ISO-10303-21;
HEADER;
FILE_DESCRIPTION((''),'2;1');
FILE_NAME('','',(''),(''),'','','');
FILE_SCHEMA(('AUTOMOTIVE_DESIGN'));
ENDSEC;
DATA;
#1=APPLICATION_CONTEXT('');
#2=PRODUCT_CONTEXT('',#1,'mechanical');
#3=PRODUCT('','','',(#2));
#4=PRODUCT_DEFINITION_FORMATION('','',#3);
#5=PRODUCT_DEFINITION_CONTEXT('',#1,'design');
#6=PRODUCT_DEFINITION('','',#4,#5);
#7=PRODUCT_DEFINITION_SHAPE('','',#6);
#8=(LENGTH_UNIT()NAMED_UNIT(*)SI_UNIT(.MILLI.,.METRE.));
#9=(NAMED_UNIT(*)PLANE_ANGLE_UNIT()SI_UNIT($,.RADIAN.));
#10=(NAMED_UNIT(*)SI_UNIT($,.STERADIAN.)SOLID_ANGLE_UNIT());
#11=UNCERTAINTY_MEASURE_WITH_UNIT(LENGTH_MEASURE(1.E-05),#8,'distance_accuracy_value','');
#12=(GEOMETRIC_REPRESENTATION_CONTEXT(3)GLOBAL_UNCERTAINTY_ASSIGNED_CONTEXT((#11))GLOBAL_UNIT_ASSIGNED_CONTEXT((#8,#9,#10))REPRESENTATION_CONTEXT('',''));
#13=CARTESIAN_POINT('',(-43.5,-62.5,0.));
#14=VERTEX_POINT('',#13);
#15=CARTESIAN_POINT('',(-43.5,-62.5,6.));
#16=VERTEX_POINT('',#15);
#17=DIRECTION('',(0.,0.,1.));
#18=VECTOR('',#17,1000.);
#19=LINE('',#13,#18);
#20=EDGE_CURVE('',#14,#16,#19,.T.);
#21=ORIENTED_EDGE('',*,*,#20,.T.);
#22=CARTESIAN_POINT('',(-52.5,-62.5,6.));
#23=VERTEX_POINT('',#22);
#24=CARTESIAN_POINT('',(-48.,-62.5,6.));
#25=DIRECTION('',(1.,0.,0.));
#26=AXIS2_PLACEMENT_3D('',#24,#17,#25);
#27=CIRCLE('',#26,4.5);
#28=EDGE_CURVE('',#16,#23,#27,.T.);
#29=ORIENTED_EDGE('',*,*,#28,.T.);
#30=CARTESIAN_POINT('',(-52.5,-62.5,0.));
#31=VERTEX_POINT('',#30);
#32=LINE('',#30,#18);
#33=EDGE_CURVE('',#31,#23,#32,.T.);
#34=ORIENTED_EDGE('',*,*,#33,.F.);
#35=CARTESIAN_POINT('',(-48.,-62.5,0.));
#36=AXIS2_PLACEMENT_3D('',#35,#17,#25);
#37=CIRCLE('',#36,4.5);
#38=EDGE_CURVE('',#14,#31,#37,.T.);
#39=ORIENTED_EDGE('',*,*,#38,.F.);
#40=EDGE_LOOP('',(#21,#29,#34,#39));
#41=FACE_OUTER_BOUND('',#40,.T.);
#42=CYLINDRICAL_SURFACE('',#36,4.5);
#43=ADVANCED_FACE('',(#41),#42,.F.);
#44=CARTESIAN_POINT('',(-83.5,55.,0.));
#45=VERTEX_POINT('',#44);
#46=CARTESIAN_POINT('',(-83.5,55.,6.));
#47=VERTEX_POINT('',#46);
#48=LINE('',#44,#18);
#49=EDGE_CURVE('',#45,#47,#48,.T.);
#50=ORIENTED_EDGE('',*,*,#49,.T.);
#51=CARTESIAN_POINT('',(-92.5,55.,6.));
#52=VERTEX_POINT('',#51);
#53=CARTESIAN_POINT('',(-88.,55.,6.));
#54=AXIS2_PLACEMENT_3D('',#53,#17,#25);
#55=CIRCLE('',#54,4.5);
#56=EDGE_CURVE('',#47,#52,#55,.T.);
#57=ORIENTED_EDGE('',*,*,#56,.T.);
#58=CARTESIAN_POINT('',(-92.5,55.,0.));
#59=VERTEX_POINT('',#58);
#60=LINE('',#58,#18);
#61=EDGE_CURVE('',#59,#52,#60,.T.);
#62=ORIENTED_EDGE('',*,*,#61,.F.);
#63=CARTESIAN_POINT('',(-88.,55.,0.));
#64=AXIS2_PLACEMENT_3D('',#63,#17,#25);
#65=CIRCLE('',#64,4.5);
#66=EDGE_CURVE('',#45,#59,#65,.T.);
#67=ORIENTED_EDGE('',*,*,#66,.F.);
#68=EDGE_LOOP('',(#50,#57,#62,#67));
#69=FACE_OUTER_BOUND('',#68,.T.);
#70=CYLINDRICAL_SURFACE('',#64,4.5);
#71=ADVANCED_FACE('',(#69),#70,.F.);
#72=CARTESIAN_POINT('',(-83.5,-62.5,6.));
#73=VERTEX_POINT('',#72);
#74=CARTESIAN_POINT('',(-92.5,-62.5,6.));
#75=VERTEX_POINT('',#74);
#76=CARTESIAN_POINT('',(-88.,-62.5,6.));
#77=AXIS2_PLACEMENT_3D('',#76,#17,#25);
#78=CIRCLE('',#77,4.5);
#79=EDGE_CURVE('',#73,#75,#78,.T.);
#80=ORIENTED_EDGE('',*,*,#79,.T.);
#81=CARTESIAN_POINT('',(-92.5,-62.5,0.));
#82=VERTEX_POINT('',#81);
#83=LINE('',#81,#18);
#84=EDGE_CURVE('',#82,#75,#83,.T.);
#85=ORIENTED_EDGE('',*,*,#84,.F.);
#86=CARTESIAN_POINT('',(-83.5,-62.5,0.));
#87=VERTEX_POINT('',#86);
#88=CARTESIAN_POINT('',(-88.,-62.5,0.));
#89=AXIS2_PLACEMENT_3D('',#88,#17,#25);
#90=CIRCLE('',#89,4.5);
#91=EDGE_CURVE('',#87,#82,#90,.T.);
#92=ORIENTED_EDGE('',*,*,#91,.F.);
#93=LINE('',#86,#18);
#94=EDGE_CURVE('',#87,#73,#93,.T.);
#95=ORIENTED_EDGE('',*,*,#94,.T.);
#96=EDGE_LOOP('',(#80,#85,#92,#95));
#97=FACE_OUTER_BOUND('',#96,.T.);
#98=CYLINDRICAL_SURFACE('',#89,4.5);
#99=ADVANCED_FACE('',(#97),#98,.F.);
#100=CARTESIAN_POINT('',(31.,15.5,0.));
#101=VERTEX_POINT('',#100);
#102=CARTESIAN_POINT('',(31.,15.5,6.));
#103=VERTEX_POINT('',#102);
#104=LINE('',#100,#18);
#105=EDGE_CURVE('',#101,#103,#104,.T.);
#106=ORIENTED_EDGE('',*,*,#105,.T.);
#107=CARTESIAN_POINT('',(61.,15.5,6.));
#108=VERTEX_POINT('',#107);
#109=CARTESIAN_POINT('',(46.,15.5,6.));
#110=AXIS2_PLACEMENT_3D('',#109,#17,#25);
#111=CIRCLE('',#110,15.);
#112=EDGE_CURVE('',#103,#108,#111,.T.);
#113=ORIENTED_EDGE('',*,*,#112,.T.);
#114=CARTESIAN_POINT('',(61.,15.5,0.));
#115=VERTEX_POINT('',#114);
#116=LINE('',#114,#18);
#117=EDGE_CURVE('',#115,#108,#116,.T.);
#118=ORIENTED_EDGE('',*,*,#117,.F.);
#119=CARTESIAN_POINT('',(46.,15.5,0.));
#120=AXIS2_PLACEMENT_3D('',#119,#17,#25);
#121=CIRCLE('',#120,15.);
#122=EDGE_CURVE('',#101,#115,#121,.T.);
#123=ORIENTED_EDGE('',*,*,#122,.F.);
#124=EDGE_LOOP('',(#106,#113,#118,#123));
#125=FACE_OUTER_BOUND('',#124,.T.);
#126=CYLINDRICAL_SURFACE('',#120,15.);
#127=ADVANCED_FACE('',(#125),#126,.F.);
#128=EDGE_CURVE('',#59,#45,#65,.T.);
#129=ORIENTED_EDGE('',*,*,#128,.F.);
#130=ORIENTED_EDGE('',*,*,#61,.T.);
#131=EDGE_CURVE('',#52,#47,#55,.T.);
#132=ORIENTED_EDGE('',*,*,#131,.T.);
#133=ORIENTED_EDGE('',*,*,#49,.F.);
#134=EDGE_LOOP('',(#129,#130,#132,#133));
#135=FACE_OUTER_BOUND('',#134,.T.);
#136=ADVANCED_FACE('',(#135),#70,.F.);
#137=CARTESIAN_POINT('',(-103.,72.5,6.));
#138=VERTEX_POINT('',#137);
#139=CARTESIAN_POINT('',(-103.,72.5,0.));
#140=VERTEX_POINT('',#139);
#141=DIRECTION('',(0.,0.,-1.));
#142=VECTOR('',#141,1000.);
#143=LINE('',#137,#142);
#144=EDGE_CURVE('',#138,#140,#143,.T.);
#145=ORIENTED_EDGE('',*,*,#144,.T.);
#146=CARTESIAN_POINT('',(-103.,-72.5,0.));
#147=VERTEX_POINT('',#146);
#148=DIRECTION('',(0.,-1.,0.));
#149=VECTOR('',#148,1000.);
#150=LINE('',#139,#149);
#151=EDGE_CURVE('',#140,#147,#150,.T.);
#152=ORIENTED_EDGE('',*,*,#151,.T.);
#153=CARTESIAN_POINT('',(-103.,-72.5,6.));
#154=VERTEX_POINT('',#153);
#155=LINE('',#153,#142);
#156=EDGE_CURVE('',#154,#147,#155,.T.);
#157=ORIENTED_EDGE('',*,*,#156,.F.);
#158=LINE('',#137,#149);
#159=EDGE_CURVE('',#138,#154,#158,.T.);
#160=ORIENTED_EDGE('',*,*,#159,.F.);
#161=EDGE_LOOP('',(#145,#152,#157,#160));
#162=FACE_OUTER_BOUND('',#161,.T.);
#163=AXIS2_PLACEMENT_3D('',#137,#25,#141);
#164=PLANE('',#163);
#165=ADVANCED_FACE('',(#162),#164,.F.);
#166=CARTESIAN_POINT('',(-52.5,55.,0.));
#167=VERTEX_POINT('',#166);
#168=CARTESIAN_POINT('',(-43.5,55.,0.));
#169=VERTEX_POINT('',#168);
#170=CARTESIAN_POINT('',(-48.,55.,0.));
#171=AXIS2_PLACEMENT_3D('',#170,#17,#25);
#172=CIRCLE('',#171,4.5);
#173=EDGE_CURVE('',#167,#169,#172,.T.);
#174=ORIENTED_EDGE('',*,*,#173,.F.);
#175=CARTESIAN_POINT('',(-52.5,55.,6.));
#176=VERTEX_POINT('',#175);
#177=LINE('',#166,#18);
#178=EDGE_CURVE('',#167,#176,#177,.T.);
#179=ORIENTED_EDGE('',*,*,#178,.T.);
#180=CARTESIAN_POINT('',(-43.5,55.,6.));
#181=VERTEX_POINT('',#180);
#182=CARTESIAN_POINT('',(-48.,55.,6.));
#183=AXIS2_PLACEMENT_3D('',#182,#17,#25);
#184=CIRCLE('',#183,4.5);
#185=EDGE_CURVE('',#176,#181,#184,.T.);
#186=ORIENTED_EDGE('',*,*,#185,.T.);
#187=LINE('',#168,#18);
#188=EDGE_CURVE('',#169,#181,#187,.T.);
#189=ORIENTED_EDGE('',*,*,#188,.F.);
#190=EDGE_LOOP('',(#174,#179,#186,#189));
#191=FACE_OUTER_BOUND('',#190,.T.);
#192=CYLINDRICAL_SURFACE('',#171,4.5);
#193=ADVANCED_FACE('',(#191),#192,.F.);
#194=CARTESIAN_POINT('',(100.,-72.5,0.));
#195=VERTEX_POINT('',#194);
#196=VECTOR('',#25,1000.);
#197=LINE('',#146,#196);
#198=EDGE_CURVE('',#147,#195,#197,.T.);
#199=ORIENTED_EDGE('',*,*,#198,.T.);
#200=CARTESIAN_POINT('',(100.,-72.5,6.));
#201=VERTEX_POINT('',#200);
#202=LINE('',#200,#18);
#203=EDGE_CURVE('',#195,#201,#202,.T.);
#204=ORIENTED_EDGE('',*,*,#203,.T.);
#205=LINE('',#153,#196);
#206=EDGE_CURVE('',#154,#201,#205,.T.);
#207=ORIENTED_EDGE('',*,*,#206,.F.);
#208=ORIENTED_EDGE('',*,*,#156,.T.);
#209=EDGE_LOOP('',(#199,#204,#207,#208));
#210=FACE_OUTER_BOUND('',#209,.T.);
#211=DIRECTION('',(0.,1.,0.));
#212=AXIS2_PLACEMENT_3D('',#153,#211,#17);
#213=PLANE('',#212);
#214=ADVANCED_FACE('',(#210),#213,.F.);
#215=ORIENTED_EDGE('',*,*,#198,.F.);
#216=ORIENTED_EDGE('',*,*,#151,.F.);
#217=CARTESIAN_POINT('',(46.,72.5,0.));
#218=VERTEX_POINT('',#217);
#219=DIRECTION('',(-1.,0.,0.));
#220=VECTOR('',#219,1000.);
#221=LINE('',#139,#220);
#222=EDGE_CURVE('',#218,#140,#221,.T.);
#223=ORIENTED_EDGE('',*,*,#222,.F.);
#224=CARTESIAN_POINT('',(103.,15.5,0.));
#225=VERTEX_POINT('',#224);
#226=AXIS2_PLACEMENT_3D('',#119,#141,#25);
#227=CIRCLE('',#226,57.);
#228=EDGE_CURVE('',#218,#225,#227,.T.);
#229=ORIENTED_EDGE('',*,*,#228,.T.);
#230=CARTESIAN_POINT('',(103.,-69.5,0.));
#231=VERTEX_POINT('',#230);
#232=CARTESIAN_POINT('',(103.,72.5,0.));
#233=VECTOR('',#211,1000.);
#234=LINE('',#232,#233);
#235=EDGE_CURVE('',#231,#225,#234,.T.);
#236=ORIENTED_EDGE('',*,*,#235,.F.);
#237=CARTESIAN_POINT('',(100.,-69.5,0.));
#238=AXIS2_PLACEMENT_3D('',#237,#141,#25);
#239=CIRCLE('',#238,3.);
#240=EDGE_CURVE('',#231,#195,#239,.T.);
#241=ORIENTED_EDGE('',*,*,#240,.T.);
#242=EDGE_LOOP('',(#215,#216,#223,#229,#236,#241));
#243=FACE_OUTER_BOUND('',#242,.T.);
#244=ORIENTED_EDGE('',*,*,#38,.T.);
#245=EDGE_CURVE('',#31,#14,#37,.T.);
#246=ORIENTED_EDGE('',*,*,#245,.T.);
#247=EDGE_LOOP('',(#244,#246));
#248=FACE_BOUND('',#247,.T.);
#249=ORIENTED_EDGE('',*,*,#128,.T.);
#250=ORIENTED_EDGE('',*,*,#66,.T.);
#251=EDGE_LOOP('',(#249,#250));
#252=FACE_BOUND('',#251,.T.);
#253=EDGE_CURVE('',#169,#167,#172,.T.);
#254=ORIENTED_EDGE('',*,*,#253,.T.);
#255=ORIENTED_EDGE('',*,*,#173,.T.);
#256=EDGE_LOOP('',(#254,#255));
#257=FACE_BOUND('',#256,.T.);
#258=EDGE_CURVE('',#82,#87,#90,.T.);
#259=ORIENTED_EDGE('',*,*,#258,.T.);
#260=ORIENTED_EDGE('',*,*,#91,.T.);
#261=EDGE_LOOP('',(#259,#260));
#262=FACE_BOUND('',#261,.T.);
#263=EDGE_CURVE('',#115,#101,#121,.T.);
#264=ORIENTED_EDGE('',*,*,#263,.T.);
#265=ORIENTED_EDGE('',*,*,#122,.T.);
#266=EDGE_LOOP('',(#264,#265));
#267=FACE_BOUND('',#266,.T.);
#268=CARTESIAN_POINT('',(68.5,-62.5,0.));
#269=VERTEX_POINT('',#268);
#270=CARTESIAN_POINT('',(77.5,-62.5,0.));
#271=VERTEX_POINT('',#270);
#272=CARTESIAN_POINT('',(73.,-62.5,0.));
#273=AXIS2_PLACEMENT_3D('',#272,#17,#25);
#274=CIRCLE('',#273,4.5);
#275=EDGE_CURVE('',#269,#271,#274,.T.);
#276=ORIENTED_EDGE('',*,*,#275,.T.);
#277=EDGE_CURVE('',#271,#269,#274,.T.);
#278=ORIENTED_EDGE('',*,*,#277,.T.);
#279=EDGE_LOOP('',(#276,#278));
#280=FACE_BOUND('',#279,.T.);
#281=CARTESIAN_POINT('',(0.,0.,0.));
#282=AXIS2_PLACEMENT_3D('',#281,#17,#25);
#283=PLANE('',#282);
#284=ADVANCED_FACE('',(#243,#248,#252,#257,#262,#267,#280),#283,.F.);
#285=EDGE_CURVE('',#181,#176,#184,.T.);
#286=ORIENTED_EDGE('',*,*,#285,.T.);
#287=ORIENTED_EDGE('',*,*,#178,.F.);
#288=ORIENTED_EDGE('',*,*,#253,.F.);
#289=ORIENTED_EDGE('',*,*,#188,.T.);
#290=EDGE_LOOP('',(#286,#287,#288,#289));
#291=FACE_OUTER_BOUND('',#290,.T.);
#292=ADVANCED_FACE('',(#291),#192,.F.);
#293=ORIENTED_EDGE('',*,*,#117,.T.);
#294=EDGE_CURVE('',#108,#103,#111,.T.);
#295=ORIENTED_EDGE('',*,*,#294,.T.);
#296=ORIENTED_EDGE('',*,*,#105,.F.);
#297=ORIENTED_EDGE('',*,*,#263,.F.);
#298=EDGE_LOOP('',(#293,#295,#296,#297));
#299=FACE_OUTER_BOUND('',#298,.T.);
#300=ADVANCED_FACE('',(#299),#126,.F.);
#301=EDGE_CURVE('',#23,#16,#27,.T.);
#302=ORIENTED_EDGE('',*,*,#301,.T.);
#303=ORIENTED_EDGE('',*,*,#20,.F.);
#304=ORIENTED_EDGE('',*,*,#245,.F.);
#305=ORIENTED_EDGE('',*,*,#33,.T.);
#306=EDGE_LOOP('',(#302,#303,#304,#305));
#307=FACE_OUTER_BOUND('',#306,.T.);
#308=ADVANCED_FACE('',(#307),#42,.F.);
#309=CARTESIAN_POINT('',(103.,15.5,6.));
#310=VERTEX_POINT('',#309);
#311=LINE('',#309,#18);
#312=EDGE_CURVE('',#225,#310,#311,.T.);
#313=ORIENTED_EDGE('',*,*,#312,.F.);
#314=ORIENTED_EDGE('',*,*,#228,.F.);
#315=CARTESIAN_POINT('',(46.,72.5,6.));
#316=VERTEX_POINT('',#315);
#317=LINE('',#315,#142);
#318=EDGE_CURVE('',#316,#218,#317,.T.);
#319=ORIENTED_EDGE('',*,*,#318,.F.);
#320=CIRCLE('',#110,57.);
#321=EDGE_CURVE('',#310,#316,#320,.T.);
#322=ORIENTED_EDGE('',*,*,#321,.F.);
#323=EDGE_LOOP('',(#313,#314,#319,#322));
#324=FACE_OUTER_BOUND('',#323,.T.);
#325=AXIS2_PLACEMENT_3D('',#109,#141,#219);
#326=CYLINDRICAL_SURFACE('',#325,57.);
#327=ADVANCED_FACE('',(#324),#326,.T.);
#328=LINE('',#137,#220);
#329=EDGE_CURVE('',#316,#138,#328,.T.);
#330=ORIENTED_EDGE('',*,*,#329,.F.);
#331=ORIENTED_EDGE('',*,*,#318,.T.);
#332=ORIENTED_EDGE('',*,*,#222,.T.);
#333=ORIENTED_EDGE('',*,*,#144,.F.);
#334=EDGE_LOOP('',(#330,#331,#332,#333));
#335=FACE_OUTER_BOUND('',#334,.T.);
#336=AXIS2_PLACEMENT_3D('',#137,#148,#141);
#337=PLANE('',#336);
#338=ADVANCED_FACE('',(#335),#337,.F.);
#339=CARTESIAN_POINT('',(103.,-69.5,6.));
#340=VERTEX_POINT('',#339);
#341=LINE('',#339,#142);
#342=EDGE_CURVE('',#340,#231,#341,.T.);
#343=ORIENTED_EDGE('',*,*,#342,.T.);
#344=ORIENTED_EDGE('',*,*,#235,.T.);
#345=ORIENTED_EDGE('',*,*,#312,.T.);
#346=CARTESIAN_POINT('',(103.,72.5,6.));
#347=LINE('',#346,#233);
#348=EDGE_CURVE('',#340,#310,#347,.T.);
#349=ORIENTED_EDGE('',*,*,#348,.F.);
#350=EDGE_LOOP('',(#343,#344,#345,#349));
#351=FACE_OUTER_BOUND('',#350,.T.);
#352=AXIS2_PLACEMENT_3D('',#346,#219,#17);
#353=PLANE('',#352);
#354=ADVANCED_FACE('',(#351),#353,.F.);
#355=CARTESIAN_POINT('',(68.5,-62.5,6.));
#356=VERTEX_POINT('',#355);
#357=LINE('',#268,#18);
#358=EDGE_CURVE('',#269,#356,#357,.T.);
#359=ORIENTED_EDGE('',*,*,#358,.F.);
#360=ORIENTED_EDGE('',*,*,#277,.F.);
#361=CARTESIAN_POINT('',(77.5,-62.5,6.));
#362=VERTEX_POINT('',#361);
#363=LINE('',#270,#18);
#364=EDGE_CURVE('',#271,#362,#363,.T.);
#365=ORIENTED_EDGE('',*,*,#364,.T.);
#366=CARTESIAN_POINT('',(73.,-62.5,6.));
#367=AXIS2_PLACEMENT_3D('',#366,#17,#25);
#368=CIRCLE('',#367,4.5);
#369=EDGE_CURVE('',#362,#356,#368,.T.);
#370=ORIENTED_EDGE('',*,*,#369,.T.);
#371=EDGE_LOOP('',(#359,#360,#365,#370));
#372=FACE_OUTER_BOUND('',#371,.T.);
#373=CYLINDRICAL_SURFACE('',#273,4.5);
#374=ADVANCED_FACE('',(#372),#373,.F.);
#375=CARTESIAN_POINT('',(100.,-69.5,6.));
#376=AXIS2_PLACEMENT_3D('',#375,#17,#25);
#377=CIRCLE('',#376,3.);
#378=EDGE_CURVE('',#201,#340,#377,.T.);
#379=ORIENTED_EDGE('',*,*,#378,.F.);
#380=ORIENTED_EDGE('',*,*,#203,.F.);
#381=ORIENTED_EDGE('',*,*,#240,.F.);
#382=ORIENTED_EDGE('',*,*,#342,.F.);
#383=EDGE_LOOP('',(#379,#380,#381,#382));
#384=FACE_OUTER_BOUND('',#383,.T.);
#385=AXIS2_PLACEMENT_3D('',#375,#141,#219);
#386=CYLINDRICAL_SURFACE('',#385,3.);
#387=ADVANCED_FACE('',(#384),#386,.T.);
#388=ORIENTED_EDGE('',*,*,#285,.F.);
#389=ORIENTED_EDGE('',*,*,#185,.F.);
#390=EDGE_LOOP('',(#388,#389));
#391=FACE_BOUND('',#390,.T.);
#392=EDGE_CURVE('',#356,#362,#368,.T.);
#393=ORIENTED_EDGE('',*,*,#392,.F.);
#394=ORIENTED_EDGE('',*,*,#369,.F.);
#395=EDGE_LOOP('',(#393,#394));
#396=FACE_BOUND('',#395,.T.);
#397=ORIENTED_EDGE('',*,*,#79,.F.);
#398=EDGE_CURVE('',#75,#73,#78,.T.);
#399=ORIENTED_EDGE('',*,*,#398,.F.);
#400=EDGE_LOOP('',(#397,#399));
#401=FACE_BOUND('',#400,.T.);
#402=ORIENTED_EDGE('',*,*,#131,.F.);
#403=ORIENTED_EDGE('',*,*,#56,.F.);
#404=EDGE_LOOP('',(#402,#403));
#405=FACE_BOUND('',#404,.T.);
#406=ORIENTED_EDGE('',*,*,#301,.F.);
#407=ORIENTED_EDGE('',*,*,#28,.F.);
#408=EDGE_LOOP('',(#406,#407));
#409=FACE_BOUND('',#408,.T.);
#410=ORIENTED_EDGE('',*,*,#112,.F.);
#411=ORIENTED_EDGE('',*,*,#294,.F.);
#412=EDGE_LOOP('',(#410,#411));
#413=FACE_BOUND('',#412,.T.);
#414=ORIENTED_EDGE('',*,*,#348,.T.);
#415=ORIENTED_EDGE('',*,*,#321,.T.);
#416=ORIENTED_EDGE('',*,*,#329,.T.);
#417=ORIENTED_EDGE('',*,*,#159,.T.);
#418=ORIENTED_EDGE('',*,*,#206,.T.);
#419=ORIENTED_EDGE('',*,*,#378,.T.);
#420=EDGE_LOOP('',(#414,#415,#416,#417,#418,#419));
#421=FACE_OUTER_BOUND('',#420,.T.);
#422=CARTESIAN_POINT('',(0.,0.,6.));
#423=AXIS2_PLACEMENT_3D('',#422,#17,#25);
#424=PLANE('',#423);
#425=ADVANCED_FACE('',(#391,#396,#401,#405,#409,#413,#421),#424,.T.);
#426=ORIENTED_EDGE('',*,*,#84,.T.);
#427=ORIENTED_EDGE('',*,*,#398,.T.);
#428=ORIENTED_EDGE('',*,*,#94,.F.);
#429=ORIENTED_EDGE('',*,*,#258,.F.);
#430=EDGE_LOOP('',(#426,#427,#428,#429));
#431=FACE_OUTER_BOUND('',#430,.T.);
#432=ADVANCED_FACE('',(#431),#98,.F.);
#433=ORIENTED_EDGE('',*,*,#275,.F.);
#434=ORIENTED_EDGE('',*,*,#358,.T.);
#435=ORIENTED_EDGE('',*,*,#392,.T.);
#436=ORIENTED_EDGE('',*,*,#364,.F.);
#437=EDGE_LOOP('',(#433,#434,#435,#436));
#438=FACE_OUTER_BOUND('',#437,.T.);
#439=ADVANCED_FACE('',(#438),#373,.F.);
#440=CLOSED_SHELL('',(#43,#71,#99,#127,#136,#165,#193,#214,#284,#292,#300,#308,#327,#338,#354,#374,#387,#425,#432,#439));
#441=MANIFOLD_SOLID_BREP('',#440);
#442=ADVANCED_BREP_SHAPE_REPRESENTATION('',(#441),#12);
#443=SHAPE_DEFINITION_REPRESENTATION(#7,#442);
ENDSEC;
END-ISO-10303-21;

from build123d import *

# Parameters (mm, degrees)
SKETCH_1_W          = 206
SKETCH_1_H          = 145
EXTRUDE_1_DEPTH     = 6
SKETCH_3_R          = 4.5
CUT_EXTRUDE_2_DEPTH = 127.100158604
SKETCH_4_R          = 15
CUT_EXTRUDE_3_DEPTH = 127.100158604
FILLET_1_R          = 57
SKETCH_11_R         = 4.5
CUT_EXTRUDE_6_DEPTH = 127.100158604
FILLET_5_R          = 3


with BuildPart() as part:
    # 草图1 → 凸台-拉伸1 (new body)
    with BuildSketch(Plane.XY):
        Rectangle(SKETCH_1_W, SKETCH_1_H)
    extrude(amount=EXTRUDE_1_DEPTH)

    # 草图3 → 切除-拉伸2 (cut, through all)
    with BuildSketch(Plane.XY.offset(6)):
        with Locations((-88, 55)):
            Circle(SKETCH_3_R)
        with Locations((-48, 55)):
            Circle(SKETCH_3_R)
        with Locations((-88, -62.5)):
            Circle(SKETCH_3_R)
        with Locations((-48, -62.5)):
            Circle(SKETCH_3_R)
    extrude(amount=-CUT_EXTRUDE_2_DEPTH, mode=Mode.SUBTRACT)

    # 草图4 → 切除-拉伸3 (cut, through all)
    with BuildSketch(Plane.XY.offset(6)):
        with Locations((46, 15.5)):
            Circle(SKETCH_4_R)
    extrude(amount=-CUT_EXTRUDE_3_DEPTH, mode=Mode.SUBTRACT)

    # 圆角1
    fillet_1_edges = [part.edges().sort_by_distance(p)[0] for p in [
        (103, 72.5, 3),
    ]]
    fillet(fillet_1_edges, radius=FILLET_1_R)

    # 草图11 → 切除-拉伸6 (cut, through all)
    with BuildSketch(Plane.XY.offset(6)):
        with Locations((73, -62.5)):
            Circle(SKETCH_11_R)
    extrude(amount=-CUT_EXTRUDE_6_DEPTH, mode=Mode.SUBTRACT)

    # 圆角5
    fillet_5_edges = [part.edges().sort_by_distance(p)[0] for p in [
        (103, -72.5, 3),
    ]]
    fillet(fillet_5_edges, radius=FILLET_5_R)


solid = part.part
